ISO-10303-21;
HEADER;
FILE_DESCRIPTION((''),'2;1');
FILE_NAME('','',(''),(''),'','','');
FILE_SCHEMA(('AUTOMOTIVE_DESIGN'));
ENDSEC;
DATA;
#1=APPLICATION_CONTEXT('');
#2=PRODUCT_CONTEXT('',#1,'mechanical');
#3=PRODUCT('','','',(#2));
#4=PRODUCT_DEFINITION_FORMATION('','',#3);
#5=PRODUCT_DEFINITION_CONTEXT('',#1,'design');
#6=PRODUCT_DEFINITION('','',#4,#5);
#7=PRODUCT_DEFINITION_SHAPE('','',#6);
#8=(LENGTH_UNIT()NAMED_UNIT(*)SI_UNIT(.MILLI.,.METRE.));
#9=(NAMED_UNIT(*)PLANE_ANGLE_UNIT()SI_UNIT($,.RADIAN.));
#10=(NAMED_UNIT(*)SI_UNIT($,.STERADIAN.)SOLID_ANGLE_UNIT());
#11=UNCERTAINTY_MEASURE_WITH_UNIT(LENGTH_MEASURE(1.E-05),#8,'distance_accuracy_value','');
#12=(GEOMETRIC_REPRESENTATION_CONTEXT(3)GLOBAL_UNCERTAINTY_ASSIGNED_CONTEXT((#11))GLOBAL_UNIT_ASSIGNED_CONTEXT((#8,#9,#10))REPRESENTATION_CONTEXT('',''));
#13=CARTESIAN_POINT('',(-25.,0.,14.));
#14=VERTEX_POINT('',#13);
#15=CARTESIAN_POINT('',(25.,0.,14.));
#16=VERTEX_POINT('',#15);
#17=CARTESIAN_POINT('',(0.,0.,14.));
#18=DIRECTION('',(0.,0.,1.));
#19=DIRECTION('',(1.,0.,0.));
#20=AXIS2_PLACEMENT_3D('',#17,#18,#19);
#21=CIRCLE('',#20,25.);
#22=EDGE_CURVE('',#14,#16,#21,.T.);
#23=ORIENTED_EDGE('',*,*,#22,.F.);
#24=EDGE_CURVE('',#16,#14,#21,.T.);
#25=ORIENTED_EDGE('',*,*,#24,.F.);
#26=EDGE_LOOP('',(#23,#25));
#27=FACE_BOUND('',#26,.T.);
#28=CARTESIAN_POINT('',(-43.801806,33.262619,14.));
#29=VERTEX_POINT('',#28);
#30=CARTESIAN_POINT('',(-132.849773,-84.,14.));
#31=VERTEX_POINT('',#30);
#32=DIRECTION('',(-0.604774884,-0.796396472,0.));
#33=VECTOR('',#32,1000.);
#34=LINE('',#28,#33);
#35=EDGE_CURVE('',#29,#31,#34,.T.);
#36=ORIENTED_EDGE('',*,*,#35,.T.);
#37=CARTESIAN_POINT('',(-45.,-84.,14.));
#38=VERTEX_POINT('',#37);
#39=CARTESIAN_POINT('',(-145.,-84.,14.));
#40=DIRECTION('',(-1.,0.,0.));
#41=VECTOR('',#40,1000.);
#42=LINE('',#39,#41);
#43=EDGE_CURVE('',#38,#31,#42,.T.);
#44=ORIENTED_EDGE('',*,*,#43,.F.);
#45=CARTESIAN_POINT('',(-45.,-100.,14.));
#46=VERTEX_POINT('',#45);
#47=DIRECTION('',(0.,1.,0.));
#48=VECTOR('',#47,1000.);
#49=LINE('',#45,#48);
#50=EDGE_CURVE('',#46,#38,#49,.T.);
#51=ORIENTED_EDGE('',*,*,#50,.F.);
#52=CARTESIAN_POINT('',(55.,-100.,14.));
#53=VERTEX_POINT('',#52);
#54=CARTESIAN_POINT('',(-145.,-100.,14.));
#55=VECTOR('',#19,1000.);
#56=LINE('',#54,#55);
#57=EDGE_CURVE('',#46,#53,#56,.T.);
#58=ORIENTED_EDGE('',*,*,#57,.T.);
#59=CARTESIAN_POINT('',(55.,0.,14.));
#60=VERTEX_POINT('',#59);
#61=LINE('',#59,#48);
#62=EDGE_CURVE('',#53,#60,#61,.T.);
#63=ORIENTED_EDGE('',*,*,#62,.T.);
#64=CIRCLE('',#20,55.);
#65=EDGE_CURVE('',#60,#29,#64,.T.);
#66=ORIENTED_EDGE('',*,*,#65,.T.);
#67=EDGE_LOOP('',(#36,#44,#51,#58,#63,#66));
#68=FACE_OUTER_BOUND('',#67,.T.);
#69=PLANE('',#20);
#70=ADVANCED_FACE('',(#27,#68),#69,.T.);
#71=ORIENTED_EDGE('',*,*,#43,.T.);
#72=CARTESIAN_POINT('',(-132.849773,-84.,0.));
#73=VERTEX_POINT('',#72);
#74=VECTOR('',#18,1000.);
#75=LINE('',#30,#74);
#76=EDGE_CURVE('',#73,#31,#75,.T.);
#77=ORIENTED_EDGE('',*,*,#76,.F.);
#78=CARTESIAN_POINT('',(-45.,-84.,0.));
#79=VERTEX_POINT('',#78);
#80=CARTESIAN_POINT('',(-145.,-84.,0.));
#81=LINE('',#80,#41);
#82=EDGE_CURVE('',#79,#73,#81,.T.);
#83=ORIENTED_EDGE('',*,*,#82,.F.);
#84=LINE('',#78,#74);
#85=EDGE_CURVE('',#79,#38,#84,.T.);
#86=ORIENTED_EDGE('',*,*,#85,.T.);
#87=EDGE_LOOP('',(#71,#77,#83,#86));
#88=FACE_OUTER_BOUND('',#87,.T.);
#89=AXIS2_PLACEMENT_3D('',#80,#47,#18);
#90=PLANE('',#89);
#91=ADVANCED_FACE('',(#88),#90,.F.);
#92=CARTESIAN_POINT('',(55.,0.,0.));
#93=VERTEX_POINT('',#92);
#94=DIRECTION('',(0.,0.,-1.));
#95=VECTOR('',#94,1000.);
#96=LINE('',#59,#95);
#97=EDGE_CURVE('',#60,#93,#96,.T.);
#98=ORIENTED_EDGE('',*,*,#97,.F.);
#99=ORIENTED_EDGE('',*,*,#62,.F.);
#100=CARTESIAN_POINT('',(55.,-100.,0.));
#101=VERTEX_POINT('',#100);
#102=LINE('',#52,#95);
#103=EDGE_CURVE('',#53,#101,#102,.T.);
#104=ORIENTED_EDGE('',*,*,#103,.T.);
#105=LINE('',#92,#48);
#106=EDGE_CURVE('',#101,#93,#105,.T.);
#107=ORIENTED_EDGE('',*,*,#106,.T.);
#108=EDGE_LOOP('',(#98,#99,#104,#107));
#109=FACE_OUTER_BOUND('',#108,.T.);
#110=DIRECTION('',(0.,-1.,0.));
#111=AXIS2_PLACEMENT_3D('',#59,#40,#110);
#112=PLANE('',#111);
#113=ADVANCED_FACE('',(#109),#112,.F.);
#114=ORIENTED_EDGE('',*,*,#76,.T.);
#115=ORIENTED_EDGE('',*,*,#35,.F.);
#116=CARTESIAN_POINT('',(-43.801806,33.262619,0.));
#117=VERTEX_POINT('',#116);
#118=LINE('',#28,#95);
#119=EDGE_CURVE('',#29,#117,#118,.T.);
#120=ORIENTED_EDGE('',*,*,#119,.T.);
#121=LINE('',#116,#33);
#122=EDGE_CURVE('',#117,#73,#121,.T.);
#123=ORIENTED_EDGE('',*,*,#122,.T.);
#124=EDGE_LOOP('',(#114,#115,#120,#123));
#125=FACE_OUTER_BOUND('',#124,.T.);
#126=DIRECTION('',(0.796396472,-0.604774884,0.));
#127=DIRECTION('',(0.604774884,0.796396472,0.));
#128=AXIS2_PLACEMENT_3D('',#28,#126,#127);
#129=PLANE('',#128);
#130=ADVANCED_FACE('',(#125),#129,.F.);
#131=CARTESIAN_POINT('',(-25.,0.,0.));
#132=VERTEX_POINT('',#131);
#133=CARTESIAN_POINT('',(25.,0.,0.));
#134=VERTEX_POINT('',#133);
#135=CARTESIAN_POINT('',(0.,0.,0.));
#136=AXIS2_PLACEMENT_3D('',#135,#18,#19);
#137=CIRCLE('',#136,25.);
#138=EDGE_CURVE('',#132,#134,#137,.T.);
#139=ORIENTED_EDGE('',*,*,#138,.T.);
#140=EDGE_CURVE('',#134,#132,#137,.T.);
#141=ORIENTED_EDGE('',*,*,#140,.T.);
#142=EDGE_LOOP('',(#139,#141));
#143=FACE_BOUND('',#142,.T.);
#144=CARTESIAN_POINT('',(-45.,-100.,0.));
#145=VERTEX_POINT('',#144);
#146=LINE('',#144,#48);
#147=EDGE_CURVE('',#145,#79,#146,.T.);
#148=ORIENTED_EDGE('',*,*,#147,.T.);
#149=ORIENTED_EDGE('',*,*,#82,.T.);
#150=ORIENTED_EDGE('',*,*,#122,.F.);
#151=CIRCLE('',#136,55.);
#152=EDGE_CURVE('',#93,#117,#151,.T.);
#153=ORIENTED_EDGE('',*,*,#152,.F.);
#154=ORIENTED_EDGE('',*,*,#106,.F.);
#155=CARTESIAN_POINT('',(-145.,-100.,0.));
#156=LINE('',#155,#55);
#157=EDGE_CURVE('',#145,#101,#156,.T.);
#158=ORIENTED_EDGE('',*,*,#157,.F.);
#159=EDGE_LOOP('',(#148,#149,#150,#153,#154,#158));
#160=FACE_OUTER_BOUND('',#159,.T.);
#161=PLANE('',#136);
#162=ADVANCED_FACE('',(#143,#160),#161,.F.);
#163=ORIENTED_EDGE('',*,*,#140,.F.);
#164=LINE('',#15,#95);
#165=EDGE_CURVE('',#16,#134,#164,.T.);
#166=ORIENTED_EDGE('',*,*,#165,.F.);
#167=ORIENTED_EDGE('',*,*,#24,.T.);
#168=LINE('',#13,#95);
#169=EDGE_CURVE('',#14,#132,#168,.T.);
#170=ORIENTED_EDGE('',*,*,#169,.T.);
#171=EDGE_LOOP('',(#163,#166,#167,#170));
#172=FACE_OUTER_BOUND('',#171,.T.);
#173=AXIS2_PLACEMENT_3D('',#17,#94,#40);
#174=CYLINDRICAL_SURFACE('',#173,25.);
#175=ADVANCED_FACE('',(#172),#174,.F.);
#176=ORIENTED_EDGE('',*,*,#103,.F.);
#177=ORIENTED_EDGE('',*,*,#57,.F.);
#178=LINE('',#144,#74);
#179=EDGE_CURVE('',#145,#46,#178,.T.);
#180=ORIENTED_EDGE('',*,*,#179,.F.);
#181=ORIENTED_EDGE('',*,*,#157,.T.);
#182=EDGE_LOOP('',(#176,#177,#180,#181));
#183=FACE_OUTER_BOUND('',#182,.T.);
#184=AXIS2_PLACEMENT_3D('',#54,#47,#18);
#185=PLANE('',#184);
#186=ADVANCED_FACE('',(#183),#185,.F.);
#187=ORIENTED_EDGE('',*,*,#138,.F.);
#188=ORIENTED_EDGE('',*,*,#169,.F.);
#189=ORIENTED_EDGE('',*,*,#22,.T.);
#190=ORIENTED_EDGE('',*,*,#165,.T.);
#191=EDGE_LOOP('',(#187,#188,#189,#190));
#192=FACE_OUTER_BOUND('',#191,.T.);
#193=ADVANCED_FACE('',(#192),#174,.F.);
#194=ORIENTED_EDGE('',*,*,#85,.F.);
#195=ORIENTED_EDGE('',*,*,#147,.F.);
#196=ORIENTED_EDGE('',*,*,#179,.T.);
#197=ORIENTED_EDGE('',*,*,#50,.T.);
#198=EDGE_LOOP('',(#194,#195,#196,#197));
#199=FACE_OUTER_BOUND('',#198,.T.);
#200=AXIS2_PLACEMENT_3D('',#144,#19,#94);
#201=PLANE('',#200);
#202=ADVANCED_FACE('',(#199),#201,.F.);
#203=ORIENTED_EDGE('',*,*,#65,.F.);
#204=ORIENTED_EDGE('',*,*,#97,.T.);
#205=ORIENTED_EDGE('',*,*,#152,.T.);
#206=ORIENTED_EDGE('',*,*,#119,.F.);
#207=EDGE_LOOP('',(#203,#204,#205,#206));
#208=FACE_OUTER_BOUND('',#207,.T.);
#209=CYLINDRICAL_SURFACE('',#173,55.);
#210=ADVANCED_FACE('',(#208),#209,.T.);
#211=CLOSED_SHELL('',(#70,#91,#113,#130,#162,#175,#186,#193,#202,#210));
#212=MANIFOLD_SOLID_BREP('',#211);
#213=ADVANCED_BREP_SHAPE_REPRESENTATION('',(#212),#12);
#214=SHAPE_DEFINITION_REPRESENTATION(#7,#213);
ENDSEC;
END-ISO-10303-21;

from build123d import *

# Parameters (mm, degrees)
SKETCH1_R           = 25
BOSS_EXTRUDE1_DEPTH = 14
SKETCH2_W           = 100
SKETCH2_H           = 16
CUT_EXTRUDE1_DEPTH  = 177.694651872


with BuildPart() as part:
    # Sketch1 → Boss-Extrude1 (new body)
    with BuildSketch(Plane.XY):
        with BuildLine():
            Line((-43.801805937, 33.262618608), (-145, -100))
            Line((-145, -100), (55, -100))
            Line((55, -100), (55, 0))
            ThreePointArc((55, 0), (17.548513804, 52.125326505), (-43.801805937, 33.262618608))
        make_face()
        Circle(SKETCH1_R, mode=Mode.SUBTRACT)
    extrude(amount=BOSS_EXTRUDE1_DEPTH)

    # Sketch2 → Cut-Extrude1 (cut, through all)
    with BuildSketch(Plane.XY.offset(14)):
        with Locations((-95, -92)):
            Rectangle(SKETCH2_W, SKETCH2_H)
    extrude(amount=-CUT_EXTRUDE1_DEPTH, mode=Mode.SUBTRACT)


solid = part.part
